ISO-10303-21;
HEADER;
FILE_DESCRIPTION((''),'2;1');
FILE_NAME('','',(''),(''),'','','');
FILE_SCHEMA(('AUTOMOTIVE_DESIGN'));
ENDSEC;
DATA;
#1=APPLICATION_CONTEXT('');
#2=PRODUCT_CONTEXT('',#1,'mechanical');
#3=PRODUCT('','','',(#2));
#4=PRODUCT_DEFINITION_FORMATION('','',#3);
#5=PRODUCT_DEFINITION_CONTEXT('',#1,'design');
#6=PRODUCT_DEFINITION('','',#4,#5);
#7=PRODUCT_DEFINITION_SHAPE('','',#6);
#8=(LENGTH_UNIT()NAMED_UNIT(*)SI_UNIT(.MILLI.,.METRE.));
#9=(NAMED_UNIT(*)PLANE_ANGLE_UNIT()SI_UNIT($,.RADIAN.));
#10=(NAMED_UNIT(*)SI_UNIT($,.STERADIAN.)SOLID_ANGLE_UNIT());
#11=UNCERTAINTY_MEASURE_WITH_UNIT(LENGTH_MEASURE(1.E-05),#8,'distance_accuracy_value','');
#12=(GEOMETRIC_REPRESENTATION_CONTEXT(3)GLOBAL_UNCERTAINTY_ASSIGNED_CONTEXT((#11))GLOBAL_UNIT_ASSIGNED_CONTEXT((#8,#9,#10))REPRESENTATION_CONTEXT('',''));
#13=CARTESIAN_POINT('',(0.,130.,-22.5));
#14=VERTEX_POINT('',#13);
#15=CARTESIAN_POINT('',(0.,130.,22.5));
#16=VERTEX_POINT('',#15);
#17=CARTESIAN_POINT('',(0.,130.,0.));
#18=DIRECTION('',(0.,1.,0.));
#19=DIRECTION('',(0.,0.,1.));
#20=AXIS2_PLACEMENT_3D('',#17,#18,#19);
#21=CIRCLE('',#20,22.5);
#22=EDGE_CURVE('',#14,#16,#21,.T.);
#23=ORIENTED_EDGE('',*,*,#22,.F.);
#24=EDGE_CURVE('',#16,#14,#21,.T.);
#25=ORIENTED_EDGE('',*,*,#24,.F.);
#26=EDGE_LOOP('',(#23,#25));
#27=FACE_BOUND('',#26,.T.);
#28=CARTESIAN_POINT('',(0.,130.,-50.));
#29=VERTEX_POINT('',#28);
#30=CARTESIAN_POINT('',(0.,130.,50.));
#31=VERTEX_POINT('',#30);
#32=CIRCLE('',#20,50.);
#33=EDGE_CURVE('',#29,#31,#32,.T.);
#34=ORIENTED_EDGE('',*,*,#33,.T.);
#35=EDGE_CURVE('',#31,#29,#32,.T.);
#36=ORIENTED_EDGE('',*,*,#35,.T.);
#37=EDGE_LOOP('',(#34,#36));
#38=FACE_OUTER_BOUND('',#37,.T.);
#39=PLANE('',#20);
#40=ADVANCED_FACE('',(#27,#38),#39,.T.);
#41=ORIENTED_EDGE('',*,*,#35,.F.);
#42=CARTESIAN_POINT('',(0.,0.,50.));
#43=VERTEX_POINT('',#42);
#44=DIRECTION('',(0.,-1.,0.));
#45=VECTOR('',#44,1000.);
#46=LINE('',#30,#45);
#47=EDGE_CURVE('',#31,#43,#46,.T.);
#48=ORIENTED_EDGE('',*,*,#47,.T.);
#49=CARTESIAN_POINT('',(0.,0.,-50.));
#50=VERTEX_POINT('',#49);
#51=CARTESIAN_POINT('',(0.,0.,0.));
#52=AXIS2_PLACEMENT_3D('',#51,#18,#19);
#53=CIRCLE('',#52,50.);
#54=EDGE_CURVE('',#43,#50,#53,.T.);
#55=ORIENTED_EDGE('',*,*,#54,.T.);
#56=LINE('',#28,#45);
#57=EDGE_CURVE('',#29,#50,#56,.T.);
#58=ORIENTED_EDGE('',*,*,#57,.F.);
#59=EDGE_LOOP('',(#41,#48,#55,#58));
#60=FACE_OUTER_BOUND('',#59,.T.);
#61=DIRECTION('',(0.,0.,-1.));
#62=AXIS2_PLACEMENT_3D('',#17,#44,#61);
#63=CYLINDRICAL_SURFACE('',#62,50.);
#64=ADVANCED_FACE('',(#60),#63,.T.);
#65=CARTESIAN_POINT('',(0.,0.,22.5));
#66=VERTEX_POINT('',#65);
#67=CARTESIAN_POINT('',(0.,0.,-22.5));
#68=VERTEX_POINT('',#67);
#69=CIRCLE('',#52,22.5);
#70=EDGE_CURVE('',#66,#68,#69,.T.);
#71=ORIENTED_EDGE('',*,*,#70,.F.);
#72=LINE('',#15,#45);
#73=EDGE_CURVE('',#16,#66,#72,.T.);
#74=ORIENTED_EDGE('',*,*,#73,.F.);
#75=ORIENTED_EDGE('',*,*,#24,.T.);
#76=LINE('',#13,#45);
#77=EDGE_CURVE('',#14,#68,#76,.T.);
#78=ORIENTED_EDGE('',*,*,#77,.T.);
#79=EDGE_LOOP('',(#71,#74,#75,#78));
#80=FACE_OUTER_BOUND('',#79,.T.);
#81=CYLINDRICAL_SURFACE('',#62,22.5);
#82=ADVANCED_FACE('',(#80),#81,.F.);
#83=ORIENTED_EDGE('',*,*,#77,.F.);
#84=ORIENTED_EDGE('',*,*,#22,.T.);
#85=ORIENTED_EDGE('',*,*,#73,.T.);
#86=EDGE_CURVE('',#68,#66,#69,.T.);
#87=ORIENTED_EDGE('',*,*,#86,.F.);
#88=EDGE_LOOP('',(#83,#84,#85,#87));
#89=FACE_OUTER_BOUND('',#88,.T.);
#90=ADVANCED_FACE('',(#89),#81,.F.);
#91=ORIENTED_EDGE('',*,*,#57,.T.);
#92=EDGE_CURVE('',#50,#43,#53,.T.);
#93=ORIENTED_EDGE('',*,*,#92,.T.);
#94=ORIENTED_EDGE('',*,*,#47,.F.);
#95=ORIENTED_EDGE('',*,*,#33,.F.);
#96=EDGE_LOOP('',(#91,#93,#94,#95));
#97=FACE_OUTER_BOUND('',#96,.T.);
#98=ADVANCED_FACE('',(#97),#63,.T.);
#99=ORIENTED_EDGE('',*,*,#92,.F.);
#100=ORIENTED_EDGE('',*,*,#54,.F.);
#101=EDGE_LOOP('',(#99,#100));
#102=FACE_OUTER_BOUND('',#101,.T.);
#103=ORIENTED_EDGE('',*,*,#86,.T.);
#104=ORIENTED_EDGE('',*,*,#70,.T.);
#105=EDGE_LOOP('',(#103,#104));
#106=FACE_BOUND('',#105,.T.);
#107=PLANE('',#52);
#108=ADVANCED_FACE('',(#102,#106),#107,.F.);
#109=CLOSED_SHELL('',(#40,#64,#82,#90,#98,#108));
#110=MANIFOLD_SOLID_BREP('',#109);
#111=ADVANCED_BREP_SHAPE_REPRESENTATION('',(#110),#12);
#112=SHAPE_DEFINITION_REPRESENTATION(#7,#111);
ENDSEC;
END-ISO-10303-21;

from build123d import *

# Parameters (mm, degrees)
SKETCH_1_R      = 50
SKETCH_1_R_2    = 22.5
EXTRUDE_1_DEPTH = 130


with BuildPart() as part:
    # 草图1 → 凸台-拉伸1 (new body)
    with BuildSketch(Plane(origin=(0, 0, 0), x_dir=(1, 0, 0), z_dir=(0, 1, 0))):
        with Locations(Location((0, 0, 0), (0, 0, 270))):
            Circle(SKETCH_1_R)
        with Locations(Location((0, 0, 0), (0, 0, 270))):
            Circle(SKETCH_1_R_2, mode=Mode.SUBTRACT)
    extrude(amount=EXTRUDE_1_DEPTH)


solid = part.part
